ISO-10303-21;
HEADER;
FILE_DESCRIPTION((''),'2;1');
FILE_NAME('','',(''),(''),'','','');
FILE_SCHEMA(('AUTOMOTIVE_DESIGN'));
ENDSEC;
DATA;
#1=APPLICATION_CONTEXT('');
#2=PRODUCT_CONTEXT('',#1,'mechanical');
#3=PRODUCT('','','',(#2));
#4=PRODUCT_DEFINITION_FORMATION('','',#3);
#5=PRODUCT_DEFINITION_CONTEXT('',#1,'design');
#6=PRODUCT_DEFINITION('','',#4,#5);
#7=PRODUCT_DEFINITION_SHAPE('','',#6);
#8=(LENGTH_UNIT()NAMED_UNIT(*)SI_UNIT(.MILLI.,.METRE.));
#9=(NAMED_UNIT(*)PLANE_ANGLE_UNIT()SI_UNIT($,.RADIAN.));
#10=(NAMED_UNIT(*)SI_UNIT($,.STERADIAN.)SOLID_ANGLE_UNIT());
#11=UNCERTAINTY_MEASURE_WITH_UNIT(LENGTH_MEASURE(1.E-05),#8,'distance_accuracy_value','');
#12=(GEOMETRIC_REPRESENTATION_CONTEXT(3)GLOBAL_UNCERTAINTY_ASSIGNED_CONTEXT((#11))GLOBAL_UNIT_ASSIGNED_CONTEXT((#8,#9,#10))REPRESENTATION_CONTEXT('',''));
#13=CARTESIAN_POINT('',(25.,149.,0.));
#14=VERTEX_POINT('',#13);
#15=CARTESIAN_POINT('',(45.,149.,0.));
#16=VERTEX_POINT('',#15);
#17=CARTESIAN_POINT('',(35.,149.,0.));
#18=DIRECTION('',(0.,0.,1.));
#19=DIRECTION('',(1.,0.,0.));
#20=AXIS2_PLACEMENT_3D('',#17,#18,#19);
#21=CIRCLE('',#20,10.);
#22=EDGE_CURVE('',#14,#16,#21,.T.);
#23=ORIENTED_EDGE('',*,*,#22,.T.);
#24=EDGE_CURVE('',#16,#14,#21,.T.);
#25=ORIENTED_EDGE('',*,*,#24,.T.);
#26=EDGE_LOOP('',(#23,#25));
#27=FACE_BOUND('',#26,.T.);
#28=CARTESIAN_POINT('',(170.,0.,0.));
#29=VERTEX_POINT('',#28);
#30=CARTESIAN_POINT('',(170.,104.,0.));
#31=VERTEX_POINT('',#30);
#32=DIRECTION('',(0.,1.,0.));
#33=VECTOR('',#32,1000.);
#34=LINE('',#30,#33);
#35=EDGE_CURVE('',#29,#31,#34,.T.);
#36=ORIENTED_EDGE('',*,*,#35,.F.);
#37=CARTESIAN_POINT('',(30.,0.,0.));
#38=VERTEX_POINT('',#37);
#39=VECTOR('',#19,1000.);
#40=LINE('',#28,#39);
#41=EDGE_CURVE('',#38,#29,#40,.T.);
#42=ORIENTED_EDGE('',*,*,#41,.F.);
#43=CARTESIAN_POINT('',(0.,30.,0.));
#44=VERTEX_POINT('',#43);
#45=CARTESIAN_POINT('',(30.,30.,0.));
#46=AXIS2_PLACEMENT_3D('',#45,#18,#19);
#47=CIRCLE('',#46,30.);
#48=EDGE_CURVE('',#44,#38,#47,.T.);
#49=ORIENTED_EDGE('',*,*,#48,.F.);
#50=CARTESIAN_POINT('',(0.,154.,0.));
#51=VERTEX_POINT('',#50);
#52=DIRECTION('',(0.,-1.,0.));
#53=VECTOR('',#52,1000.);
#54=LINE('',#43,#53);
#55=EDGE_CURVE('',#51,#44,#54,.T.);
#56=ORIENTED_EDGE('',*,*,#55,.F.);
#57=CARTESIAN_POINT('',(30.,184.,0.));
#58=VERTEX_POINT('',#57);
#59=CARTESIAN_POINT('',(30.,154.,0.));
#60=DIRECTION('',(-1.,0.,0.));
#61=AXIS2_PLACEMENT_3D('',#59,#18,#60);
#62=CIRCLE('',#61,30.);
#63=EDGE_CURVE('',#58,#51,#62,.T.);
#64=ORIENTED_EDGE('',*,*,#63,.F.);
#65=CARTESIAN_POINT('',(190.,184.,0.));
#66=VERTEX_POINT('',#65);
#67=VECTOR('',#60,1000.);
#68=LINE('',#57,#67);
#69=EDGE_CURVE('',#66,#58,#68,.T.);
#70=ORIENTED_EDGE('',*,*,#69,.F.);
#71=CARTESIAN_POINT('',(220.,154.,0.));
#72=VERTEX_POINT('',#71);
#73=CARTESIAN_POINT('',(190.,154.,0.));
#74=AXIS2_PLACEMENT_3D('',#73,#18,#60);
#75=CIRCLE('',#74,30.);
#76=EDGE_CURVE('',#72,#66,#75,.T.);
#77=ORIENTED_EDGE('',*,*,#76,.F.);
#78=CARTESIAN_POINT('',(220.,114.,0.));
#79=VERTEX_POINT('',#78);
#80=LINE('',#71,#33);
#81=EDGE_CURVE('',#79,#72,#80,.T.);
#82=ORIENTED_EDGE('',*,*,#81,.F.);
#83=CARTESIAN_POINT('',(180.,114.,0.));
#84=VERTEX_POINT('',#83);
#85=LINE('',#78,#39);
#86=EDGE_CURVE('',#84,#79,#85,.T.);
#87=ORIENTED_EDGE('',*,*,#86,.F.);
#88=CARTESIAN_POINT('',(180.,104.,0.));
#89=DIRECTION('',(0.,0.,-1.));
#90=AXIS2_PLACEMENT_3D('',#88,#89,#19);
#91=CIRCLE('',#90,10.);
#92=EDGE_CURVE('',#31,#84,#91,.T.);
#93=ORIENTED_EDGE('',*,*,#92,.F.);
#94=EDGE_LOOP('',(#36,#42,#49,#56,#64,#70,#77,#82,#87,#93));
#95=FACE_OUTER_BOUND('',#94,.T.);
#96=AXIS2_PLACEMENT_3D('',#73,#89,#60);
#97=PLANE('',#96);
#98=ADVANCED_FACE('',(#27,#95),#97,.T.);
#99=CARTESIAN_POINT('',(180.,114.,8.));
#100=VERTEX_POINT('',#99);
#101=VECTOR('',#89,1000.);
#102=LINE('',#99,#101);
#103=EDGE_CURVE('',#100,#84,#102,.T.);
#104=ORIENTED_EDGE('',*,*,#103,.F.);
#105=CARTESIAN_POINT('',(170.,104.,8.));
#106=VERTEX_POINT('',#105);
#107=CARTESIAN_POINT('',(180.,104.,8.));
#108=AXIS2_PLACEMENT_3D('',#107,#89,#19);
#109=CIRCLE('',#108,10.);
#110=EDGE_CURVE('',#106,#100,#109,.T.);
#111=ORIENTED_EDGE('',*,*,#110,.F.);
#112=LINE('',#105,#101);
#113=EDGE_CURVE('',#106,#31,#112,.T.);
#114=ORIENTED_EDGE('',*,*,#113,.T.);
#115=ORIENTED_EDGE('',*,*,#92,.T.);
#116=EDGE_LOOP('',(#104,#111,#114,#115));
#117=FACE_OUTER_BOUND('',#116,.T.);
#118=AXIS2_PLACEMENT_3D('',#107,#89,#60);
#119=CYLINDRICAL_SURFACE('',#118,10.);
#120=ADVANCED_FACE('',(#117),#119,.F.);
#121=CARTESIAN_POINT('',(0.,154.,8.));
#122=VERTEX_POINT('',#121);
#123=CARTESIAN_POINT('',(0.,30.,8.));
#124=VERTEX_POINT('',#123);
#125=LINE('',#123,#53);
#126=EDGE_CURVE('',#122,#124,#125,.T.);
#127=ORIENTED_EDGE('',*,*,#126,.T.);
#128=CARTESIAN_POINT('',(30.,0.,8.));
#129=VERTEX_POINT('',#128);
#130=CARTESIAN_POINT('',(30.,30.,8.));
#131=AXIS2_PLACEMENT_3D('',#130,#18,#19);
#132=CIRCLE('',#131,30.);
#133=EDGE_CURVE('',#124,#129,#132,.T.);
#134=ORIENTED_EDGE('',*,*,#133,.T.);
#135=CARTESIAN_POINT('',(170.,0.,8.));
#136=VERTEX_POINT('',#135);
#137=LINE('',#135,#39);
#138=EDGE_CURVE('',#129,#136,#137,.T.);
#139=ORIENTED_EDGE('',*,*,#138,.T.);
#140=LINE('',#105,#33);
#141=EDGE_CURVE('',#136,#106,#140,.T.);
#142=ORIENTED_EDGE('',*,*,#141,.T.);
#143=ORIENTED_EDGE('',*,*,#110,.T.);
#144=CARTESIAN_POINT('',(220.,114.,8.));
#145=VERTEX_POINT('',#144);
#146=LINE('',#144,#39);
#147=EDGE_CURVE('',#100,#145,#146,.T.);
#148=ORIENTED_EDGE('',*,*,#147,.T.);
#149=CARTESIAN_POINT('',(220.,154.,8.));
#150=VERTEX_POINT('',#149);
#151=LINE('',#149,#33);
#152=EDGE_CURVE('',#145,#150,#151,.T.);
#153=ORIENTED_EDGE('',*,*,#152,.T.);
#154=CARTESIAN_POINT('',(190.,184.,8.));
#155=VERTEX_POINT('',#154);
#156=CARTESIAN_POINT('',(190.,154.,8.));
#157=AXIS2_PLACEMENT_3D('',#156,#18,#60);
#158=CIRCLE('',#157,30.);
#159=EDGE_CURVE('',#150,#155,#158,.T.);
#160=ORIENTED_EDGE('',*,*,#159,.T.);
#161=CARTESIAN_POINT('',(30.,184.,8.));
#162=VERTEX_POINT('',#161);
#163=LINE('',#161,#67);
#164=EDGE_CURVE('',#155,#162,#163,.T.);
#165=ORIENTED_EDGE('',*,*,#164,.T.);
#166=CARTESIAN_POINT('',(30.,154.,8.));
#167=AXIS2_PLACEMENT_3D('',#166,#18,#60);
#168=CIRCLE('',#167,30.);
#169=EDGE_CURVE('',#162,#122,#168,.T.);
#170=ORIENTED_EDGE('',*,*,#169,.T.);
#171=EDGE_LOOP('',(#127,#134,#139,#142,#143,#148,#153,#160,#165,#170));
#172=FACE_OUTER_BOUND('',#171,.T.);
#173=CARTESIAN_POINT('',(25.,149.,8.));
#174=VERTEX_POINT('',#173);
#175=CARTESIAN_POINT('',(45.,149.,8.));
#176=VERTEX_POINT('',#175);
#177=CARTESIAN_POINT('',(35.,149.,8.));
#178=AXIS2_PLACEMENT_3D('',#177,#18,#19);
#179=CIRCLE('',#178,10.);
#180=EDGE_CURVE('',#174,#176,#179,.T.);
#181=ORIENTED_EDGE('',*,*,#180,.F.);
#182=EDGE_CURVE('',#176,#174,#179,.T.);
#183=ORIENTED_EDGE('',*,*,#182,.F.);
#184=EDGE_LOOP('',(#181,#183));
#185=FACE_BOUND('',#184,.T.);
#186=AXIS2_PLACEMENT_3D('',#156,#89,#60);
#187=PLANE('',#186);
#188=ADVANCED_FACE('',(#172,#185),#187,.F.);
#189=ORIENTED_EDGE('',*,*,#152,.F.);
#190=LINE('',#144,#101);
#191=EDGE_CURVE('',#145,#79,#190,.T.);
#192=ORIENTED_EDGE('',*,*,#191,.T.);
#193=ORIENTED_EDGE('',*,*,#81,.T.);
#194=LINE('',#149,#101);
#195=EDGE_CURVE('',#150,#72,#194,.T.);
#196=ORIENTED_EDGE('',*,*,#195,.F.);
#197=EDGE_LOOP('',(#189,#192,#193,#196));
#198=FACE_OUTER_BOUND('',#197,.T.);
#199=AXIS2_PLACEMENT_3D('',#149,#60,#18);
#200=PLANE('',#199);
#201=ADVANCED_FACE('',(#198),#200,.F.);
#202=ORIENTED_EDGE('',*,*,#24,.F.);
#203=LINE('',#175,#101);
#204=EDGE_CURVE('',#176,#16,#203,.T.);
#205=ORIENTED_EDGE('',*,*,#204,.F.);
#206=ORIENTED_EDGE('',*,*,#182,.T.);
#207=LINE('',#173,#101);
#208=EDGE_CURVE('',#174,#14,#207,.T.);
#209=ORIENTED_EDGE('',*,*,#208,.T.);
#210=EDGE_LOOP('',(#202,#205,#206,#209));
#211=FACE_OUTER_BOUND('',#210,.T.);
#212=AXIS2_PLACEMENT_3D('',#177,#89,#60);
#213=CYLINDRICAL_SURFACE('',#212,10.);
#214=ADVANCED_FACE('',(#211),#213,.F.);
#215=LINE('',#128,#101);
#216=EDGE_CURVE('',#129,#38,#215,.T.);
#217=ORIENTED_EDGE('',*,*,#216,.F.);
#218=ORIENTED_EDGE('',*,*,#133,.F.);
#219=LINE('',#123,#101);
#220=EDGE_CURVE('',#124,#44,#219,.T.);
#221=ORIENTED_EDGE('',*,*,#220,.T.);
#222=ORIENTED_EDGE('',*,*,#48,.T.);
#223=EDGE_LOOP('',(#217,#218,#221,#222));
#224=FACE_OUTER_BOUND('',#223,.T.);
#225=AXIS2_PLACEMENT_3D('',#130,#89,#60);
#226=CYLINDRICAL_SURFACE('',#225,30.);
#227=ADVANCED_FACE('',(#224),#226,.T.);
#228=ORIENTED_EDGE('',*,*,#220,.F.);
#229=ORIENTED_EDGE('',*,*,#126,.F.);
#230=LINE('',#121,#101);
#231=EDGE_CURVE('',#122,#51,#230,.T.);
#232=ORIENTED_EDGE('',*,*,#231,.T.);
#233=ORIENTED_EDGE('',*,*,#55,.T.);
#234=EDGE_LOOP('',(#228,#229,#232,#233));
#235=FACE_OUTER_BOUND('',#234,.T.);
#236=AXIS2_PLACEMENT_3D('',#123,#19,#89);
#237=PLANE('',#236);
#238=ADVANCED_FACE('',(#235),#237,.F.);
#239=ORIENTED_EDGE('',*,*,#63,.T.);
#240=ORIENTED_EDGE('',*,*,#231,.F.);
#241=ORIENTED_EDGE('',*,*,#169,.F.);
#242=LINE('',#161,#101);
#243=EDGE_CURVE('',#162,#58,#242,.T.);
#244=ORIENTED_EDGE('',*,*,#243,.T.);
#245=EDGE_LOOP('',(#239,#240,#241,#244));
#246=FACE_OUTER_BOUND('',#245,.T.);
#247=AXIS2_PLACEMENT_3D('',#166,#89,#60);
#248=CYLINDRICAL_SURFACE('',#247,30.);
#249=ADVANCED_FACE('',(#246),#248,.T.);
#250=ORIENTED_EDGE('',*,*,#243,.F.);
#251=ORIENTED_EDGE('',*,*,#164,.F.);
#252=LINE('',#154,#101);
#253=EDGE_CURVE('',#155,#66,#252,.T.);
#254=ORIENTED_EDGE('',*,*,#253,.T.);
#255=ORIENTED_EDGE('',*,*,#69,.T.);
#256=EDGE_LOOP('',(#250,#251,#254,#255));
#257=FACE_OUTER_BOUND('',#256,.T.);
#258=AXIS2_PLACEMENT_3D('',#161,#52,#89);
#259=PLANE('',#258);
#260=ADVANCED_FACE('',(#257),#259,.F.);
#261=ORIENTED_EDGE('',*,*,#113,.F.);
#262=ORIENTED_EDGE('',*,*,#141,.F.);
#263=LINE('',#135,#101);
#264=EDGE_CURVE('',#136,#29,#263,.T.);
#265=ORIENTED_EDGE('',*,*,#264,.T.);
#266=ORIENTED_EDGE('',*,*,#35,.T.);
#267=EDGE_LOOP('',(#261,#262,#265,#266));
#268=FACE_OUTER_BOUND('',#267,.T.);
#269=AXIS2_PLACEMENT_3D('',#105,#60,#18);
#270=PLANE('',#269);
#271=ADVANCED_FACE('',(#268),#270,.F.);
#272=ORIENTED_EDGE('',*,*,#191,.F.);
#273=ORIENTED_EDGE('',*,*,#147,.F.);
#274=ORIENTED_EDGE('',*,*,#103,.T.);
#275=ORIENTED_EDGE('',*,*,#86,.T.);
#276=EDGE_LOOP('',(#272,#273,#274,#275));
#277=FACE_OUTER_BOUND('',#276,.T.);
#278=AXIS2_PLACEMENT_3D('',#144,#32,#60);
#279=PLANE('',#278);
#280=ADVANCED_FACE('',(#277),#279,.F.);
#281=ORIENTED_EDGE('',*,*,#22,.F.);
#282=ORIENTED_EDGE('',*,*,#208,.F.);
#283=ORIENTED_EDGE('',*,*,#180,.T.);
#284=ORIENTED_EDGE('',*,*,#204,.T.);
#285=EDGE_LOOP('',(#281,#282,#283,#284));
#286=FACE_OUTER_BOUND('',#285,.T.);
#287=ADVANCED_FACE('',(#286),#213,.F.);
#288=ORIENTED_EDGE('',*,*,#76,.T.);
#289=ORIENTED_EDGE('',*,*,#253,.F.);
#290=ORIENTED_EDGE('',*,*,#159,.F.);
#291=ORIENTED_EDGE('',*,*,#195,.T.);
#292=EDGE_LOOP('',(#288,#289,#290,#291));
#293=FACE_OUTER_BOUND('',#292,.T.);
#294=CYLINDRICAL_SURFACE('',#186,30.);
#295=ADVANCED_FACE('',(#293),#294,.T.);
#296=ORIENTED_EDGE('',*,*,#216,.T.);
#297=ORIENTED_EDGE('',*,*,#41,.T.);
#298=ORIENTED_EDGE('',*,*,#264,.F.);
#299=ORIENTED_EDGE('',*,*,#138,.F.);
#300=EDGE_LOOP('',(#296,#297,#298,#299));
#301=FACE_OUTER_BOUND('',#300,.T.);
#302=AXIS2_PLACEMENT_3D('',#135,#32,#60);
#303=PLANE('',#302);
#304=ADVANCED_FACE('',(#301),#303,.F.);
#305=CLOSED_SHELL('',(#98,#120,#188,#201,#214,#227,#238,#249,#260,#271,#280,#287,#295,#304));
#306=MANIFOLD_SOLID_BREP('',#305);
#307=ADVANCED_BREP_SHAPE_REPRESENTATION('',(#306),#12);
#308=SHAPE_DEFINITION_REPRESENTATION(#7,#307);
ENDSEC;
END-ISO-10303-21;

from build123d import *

# Parameters (mm, degrees)
SKETCH_1_R      = 10
EXTRUDE_1_DEPTH = 8


with BuildPart() as part:
    # 草图1 → 凸台-拉伸1 (new body)
    with BuildSketch(Plane.XY):
        with BuildLine():
            Line((0, 30), (0, 154))
            ThreePointArc((0, 154), (8.786796564, 175.213203436), (30, 184))
            Line((30, 184), (190, 184))
            ThreePointArc((190, 184), (211.213203436, 175.213203436), (220, 154))
            Line((220, 154), (220, 114))
            Line((220, 114), (180, 114))
            ThreePointArc((180, 114), (172.928932188, 111.071067812), (170, 104))
            Line((170, 104), (170, 0))
            Line((170, 0), (30, 0))
            ThreePointArc((30, 0), (8.786796564, 8.786796564), (0, 30))
        make_face()
        with Locations((35, 149)):
            Circle(SKETCH_1_R, mode=Mode.SUBTRACT)
    extrude(amount=EXTRUDE_1_DEPTH)


solid = part.part
